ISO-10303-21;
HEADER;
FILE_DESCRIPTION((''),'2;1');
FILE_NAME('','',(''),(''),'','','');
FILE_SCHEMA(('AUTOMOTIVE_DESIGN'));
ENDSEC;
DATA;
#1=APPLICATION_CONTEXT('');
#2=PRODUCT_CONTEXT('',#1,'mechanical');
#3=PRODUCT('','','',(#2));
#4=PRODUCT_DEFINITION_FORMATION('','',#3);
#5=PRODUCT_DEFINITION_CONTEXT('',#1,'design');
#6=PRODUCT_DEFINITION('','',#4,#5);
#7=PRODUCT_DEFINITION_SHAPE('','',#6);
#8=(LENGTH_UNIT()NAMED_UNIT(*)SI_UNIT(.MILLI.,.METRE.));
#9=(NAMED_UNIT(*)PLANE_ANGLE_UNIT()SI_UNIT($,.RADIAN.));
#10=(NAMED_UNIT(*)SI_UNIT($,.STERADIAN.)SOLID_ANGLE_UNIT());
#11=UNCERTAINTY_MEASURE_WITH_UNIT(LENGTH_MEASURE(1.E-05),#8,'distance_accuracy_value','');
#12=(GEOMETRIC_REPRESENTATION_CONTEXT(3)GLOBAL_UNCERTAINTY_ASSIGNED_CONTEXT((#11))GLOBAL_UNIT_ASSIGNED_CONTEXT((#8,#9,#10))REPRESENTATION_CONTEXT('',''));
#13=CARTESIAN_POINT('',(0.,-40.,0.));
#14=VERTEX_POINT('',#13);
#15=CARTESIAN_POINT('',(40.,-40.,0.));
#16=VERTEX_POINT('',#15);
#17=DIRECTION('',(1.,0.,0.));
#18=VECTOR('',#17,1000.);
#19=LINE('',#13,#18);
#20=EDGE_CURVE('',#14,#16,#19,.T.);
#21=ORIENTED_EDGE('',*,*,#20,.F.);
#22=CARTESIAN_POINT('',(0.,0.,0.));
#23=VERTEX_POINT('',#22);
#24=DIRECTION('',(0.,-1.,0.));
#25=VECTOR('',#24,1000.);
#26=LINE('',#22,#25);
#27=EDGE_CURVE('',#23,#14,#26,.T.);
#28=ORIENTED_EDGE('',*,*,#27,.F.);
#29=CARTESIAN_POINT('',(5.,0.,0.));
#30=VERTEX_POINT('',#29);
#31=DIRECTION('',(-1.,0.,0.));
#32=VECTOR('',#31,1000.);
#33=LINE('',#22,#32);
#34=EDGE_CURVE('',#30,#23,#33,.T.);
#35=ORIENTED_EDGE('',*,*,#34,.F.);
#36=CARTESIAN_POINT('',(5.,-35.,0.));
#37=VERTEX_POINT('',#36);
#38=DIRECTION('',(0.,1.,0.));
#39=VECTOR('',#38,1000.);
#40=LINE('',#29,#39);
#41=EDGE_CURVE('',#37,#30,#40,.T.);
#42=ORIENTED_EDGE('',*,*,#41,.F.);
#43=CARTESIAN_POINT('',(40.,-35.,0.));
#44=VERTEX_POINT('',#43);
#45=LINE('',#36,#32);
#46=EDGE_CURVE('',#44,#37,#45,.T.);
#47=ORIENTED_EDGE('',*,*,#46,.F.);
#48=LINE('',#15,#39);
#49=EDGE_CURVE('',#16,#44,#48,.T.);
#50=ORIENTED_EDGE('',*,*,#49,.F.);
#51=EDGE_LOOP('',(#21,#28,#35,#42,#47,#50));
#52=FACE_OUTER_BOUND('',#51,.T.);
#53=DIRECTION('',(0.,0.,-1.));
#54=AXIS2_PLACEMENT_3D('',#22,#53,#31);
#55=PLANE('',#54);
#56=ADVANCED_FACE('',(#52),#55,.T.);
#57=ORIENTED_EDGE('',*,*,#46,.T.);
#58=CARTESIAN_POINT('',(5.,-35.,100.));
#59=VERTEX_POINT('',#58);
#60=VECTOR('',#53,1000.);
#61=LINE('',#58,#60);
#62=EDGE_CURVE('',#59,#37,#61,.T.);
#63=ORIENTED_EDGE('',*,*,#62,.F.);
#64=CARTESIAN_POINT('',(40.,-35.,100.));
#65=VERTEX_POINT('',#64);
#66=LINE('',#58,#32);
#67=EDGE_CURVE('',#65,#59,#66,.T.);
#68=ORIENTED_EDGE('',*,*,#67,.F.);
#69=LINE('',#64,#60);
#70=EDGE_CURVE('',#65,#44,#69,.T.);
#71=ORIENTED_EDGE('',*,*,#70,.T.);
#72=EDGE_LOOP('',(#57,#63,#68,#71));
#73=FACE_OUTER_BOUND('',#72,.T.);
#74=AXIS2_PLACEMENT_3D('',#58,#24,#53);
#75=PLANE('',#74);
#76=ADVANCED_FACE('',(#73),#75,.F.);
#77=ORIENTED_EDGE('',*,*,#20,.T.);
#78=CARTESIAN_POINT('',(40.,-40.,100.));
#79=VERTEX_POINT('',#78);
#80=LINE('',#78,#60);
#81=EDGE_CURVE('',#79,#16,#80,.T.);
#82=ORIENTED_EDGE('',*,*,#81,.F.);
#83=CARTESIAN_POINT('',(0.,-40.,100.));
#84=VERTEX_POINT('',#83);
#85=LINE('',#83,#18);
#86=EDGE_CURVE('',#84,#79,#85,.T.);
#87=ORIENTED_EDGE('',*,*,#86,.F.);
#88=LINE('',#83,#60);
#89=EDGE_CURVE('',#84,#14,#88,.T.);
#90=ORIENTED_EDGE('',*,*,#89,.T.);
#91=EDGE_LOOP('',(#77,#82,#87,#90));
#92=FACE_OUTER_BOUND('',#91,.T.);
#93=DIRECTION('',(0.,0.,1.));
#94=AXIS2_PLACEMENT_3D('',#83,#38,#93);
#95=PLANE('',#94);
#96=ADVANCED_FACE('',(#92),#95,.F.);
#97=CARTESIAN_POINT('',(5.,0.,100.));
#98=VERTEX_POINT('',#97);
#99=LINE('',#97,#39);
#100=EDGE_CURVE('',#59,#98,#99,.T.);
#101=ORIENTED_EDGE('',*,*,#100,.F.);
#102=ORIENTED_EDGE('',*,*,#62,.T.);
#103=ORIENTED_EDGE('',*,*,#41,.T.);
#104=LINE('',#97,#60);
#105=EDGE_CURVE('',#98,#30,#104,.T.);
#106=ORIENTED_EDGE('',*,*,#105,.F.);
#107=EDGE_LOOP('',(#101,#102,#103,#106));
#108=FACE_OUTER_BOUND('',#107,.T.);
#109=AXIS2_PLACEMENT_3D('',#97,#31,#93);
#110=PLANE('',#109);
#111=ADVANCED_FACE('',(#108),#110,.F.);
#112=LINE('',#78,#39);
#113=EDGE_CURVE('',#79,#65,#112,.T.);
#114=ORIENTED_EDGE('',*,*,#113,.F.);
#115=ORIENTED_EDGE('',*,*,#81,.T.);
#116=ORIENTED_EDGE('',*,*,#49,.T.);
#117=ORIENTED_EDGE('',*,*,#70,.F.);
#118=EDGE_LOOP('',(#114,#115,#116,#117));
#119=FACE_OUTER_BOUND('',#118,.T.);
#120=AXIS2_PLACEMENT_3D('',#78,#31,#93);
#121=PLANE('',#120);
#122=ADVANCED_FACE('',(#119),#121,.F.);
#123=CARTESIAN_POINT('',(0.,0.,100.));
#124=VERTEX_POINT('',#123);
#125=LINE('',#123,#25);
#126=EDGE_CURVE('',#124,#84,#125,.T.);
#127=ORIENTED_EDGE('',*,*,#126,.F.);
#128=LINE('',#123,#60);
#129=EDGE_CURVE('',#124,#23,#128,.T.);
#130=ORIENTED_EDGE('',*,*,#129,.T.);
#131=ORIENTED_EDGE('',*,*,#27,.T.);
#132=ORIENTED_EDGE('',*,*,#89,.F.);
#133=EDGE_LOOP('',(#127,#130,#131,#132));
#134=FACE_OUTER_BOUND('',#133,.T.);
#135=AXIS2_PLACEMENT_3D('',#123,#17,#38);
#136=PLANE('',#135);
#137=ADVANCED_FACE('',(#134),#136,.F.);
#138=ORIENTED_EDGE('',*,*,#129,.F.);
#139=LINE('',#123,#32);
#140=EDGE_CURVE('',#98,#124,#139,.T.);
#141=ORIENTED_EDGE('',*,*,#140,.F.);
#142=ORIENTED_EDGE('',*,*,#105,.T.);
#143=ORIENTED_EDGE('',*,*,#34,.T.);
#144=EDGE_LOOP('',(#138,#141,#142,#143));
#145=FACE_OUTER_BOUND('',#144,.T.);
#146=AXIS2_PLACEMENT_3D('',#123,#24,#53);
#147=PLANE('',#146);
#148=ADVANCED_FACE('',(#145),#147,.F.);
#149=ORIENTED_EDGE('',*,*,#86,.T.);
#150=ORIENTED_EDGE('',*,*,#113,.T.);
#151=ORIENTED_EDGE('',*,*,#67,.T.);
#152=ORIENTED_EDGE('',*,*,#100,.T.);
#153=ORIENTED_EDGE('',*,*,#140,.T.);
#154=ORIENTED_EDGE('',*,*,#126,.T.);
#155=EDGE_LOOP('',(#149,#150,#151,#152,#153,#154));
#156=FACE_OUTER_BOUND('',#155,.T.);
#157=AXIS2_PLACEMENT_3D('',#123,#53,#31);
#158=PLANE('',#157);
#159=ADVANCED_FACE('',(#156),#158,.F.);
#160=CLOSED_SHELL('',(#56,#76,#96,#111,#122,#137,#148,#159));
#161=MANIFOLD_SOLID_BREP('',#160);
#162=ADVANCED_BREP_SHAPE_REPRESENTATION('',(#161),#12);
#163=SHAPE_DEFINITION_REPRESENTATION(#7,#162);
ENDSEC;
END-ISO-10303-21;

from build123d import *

# Parameters (mm, degrees)
EXTRUDE_1_DEPTH = 100


with BuildPart() as part:
    # 草图1 → 凸台-拉伸1 (new body)
    with BuildSketch(Plane.XY):
        Polygon((0, 0), (0, -40), (40, -40), (40, -35), (5, -35), (5, 0), align=None)
    extrude(amount=EXTRUDE_1_DEPTH)


solid = part.part
